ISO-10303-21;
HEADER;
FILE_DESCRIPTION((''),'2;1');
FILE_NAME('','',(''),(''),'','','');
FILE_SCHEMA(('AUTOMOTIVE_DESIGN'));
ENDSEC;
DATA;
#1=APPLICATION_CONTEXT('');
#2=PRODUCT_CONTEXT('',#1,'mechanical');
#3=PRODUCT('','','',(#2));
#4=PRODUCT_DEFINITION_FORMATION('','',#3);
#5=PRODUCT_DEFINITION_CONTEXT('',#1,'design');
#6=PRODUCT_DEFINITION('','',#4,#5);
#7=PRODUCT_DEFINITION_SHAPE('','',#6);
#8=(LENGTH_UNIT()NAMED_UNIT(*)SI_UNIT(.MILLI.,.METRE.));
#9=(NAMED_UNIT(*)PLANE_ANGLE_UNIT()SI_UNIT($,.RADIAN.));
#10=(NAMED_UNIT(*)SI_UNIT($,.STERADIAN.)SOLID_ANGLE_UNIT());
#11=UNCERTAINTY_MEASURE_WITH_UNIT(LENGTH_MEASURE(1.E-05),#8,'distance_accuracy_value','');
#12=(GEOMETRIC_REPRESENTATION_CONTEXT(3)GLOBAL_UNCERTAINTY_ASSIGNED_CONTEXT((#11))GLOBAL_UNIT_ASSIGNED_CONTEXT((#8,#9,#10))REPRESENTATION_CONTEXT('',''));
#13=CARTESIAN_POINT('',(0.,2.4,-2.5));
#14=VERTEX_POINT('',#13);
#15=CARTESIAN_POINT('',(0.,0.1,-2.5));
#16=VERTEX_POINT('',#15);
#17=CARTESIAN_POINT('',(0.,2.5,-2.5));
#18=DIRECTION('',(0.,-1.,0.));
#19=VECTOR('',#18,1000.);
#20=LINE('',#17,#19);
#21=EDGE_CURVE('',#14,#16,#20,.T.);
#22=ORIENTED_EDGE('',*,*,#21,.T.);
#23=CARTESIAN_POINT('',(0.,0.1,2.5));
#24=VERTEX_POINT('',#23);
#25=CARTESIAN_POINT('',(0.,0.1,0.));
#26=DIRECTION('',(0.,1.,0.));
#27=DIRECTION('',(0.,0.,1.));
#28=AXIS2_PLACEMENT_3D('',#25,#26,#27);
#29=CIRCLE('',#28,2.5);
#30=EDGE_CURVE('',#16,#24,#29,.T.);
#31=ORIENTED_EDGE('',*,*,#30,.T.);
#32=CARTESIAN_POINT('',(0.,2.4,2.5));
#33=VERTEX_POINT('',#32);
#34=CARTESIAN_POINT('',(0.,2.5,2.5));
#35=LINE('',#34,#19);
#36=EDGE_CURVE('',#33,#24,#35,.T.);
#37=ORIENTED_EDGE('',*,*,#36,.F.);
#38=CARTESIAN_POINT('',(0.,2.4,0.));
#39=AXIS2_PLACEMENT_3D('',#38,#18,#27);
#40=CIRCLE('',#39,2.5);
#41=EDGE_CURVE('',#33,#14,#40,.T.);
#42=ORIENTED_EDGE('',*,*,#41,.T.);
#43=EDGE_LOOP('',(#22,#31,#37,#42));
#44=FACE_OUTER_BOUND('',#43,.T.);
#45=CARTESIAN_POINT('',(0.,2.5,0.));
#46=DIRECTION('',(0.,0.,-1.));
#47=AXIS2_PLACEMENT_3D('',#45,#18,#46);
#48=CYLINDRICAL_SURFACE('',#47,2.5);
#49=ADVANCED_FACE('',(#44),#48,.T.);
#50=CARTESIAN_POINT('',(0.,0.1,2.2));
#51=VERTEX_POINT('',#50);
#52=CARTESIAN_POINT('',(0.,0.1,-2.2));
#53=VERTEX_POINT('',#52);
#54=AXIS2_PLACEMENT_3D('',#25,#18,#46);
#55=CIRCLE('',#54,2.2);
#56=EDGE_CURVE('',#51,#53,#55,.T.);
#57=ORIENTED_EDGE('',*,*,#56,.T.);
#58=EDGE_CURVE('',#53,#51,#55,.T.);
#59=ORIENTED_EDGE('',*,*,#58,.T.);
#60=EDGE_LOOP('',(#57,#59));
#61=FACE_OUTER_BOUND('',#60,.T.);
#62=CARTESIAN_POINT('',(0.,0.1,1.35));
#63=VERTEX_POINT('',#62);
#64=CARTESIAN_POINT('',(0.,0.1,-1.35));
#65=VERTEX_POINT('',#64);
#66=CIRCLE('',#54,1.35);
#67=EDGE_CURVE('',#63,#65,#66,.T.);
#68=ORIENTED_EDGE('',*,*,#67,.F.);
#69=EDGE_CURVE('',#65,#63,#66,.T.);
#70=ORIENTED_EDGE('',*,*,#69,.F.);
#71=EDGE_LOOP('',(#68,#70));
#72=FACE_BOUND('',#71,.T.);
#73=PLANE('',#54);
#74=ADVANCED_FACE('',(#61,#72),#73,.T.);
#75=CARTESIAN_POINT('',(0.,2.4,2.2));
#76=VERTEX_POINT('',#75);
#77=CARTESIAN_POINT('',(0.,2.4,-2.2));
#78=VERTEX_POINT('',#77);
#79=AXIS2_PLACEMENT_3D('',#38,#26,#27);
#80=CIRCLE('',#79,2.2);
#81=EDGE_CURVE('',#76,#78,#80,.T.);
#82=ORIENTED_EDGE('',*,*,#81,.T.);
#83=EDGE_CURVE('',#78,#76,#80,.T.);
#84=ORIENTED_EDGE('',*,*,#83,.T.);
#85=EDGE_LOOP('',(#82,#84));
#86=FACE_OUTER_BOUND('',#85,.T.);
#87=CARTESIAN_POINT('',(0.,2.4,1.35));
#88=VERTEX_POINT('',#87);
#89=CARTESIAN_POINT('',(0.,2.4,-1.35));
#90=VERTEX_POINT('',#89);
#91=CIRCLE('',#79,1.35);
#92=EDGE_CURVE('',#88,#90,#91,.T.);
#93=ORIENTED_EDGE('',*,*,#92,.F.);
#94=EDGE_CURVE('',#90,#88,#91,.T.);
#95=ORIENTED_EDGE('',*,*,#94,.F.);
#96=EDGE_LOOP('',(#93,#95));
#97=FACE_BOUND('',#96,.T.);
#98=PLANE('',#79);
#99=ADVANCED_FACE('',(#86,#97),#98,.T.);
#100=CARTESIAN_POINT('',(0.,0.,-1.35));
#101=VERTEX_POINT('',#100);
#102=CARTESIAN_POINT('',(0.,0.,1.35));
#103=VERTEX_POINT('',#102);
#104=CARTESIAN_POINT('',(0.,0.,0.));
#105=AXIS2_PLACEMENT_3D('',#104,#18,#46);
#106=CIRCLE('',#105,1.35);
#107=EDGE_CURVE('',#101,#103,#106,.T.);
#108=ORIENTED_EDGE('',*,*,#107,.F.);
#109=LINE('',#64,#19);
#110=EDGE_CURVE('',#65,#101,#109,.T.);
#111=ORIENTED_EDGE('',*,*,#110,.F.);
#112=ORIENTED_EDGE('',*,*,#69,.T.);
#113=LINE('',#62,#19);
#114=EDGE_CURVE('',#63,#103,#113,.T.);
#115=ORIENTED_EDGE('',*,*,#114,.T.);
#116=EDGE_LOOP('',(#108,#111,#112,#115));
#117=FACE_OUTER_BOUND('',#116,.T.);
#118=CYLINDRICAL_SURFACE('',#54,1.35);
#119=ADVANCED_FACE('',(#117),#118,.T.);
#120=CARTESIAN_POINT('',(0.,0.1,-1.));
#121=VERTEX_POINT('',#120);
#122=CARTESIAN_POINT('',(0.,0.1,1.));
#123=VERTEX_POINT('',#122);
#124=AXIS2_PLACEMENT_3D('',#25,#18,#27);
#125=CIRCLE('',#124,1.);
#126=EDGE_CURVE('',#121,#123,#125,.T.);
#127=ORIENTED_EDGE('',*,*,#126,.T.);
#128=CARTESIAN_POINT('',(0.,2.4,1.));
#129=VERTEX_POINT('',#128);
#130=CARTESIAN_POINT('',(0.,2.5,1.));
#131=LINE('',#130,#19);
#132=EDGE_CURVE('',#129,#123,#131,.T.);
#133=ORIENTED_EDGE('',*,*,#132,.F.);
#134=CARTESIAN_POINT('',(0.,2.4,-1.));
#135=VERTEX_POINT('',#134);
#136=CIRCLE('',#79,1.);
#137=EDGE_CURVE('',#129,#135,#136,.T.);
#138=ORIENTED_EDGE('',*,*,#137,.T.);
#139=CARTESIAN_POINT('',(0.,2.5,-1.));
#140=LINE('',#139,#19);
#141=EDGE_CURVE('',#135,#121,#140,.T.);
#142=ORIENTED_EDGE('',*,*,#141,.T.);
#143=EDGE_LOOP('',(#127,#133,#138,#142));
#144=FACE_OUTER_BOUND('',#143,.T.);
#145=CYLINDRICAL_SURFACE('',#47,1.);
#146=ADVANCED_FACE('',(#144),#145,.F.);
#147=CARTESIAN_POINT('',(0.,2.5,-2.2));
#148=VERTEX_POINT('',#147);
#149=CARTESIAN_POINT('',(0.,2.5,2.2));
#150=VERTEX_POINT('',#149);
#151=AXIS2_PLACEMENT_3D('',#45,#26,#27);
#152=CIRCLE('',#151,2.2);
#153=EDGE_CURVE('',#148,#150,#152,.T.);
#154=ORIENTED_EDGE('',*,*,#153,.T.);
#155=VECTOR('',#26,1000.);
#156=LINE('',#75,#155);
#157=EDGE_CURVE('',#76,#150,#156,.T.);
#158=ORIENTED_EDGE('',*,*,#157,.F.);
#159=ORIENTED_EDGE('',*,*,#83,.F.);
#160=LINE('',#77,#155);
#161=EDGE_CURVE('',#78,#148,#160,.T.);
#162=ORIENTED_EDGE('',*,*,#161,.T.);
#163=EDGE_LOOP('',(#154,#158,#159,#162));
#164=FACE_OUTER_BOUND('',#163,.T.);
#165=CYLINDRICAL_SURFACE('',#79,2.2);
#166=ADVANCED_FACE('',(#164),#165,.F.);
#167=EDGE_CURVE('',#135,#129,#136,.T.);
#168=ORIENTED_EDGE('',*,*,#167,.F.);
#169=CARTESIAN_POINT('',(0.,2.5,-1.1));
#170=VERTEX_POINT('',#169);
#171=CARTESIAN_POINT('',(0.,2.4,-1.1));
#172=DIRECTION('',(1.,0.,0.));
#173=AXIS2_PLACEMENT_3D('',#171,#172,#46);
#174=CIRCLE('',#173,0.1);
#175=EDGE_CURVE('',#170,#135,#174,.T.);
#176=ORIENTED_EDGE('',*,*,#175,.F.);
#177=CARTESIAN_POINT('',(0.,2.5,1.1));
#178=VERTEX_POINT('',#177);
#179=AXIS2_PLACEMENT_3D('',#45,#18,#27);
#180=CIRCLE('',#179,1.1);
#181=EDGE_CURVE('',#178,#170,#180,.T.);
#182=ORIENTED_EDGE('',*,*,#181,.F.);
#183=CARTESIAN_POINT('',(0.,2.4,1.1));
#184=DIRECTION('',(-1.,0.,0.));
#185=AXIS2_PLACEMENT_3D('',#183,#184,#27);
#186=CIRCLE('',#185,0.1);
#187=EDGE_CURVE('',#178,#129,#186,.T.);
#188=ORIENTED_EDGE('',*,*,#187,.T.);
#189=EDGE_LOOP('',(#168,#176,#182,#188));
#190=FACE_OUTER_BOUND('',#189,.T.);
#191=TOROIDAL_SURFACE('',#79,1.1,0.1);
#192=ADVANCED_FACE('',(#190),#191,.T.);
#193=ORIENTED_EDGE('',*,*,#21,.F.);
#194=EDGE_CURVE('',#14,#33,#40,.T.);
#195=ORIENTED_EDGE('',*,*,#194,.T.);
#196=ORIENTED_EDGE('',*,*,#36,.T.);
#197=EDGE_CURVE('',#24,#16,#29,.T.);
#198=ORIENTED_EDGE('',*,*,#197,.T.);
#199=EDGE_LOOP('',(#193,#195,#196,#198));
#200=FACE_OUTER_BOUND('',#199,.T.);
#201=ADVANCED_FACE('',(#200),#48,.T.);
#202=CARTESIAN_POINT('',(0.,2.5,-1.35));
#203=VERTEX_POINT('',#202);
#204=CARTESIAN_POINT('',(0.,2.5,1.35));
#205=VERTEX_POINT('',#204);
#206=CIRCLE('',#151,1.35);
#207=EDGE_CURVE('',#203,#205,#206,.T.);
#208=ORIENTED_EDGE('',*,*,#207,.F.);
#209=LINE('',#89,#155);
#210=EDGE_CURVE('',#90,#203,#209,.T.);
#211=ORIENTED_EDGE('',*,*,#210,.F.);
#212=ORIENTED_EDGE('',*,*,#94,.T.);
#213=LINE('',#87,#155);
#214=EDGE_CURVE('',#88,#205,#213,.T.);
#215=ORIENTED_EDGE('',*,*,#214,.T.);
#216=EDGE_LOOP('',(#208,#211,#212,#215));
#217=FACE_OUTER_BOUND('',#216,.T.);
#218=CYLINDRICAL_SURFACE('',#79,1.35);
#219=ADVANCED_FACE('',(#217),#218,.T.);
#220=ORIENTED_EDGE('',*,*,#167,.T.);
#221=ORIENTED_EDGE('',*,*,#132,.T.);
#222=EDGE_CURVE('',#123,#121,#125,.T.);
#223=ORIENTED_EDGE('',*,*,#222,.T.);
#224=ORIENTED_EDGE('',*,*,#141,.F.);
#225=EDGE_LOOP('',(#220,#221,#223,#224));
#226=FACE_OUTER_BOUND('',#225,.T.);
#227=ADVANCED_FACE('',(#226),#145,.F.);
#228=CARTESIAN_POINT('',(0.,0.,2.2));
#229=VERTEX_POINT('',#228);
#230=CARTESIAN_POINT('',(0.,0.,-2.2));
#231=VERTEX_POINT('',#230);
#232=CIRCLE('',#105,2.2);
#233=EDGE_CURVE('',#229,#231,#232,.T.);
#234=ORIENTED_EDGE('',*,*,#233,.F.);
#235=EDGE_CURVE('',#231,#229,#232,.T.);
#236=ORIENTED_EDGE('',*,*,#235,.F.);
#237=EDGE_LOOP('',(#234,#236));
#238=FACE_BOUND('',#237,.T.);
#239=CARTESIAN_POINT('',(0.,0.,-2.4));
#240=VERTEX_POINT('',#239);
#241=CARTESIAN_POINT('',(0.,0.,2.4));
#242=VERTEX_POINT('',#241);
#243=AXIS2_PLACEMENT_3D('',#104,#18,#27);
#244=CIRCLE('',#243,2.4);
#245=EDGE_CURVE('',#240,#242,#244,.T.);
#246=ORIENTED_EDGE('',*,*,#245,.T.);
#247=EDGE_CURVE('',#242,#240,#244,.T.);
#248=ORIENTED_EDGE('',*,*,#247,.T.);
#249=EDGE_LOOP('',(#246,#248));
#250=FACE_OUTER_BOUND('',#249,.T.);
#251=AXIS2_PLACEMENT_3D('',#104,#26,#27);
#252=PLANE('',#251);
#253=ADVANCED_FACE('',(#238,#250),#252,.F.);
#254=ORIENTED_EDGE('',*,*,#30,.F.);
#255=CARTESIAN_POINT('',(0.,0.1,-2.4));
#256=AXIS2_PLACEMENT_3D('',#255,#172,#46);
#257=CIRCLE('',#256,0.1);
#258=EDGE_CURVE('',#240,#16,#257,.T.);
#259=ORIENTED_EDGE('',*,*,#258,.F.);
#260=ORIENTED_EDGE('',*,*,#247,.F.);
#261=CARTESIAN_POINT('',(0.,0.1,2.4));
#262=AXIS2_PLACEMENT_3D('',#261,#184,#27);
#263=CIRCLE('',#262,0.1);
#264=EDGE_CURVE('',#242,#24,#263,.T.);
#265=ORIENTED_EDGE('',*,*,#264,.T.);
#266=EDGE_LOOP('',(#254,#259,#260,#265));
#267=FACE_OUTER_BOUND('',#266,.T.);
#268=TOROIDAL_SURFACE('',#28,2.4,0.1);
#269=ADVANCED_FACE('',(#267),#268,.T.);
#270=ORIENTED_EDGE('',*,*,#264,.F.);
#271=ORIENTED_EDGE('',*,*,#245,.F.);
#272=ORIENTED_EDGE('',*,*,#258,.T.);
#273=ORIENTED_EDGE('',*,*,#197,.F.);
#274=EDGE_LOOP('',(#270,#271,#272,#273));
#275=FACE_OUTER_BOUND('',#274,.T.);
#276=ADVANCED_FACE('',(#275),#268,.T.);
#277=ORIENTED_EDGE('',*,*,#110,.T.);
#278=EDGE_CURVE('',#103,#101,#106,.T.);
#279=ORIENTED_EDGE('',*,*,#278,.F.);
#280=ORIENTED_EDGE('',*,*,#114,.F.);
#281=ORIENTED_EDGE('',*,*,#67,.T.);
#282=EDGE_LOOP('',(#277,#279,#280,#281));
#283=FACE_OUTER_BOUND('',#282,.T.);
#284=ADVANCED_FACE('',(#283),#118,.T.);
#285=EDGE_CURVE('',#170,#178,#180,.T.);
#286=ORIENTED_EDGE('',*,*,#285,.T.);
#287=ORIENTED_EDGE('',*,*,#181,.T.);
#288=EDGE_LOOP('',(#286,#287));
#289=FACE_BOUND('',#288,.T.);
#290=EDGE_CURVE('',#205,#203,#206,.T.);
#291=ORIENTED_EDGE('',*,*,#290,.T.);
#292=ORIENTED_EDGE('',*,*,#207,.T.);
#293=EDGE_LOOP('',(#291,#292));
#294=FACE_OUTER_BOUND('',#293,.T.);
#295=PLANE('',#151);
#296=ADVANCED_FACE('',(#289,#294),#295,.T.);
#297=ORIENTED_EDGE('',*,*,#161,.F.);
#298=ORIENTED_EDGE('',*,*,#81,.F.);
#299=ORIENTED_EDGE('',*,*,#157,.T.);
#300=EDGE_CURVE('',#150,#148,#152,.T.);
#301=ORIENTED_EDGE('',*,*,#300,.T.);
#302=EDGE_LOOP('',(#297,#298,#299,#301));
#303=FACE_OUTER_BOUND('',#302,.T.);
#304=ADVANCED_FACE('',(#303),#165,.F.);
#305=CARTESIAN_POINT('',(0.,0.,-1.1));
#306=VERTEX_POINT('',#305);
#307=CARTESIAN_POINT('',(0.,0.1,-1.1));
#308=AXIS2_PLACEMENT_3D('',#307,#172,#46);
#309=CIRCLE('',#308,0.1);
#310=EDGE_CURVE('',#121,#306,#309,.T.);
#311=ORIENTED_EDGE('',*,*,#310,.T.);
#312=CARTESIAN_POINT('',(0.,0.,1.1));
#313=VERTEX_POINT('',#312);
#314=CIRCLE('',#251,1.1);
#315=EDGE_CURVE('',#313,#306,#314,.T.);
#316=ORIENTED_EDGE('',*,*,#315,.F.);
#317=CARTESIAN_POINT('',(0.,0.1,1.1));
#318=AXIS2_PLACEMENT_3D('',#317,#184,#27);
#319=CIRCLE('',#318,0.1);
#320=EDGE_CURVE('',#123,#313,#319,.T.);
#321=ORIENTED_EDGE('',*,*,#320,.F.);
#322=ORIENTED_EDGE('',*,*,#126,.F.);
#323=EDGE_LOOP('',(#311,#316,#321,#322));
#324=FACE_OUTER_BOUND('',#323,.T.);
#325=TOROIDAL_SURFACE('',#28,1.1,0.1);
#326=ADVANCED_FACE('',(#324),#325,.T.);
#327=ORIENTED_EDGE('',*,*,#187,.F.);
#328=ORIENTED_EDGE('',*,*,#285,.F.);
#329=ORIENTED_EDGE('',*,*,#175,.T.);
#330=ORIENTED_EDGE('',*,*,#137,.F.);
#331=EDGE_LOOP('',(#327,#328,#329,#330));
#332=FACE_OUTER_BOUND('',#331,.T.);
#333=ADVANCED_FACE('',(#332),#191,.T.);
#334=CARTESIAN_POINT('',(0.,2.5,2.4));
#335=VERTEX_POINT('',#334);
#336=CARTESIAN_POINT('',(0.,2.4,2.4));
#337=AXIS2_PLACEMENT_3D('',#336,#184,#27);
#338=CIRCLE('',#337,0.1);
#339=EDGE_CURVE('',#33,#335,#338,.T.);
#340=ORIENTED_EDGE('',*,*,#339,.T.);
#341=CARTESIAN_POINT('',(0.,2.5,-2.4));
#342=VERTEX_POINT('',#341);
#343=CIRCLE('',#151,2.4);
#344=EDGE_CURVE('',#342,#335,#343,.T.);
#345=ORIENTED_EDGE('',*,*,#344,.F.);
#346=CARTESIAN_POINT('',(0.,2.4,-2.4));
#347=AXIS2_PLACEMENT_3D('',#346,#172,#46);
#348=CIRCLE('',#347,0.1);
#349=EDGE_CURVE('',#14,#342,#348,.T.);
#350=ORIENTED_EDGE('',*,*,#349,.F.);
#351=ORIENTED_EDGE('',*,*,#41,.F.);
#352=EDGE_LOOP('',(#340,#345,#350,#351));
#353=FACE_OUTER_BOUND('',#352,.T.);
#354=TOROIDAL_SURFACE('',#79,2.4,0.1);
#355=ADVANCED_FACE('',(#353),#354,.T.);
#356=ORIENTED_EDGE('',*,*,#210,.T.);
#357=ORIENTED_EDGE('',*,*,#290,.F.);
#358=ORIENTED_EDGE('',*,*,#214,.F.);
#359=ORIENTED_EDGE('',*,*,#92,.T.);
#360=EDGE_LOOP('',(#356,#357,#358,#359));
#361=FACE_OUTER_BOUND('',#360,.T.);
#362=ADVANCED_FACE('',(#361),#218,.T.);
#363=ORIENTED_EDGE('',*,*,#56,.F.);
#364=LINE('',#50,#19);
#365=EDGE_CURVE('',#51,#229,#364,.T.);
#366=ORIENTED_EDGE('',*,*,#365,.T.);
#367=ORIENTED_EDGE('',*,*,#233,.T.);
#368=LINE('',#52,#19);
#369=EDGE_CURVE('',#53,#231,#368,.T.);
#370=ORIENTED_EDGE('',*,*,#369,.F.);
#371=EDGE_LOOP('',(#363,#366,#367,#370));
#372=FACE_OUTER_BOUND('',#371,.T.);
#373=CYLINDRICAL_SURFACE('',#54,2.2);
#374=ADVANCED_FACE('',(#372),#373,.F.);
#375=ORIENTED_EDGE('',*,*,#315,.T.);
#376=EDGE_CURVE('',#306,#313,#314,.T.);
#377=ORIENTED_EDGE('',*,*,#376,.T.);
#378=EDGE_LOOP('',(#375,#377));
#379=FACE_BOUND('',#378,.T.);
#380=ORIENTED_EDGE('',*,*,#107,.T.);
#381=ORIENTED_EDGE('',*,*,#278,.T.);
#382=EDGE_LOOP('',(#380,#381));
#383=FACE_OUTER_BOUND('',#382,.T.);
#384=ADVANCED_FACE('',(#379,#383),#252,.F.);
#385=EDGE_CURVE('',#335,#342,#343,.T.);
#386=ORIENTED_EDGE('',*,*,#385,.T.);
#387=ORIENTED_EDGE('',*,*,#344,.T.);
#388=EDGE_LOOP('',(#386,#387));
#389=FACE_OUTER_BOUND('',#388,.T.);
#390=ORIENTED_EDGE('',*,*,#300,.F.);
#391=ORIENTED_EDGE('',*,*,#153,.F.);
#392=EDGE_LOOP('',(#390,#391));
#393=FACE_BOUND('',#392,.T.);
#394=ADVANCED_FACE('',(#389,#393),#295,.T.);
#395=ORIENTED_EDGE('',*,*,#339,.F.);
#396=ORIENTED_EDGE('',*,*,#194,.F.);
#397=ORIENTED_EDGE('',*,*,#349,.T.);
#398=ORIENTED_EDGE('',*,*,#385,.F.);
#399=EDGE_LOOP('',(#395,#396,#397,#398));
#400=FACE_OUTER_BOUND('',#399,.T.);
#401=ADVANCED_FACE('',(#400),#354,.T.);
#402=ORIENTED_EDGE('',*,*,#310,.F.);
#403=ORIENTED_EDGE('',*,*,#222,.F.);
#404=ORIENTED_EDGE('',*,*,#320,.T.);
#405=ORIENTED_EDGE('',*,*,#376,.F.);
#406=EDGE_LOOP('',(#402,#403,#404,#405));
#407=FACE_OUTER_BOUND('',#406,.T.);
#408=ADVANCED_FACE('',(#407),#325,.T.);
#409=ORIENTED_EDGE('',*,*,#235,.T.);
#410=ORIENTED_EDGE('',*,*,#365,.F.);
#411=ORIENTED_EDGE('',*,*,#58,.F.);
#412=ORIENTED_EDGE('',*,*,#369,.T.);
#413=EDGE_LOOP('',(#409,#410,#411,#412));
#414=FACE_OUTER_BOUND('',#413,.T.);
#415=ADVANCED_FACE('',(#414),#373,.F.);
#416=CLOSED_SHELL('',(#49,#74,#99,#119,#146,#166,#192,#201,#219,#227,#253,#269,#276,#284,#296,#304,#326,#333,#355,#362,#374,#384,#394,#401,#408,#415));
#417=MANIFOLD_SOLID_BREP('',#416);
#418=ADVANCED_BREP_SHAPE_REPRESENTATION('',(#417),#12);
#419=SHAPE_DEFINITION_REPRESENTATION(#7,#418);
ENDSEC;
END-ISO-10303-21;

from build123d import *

# Parameters (mm, degrees)
SKETCH_1_R          = 2.5
SKETCH_1_R_2        = 1
EXTRUDE_1_DEPTH     = 2.5
SKETCH_2_R          = 2.2
SKETCH_2_R_2        = 1.35
CUT_EXTRUDE_1_DEPTH = 0.1
CUT_EXTRUDE_START   = -0.1
SKETCH_4_R          = 2.2
SKETCH_4_R_2        = 1.35
CUT_EXTRUDE_2_DEPTH = 0.1
FILLET_R0_1_1_R     = 0.1


with BuildPart() as part:
    # 草图1 → 凸台-拉伸1 (new body)
    with BuildSketch(Plane(origin=(0, 0, 0), x_dir=(1, 0, 0), z_dir=(0, 1, 0))):
        with Locations(Location((0, 0, 0), (0, 0, 270))):
            Circle(SKETCH_1_R)
        with Locations(Location((0, 0, 0), (0, 0, 270))):
            Circle(SKETCH_1_R_2, mode=Mode.SUBTRACT)
    extrude(amount=EXTRUDE_1_DEPTH)

    # 草图2 → 切除-拉伸1 (cut)
    with BuildSketch(Plane(origin=(0, 2.5, 0), x_dir=(1, 0, 0), z_dir=(0, 1, 0))):
        with Locations(Location((0, 0, 0), (0, 0, 270))):
            Circle(SKETCH_2_R)
        with Locations(Location((0, 0, 0), (0, 0, 270))):
            Circle(SKETCH_2_R_2, mode=Mode.SUBTRACT)
    extrude(amount=-CUT_EXTRUDE_1_DEPTH, mode=Mode.SUBTRACT)

    # 草图4 → 切除-拉伸2 (cut)
    with BuildSketch(Plane.XZ.offset(CUT_EXTRUDE_START)):
        with Locations(Location((0, 0, 0), (0, 0, 90))):
            Circle(SKETCH_4_R)
        with Locations(Location((0, 0, 0), (0, 0, 90))):
            Circle(SKETCH_4_R_2, mode=Mode.SUBTRACT)
    extrude(amount=CUT_EXTRUDE_2_DEPTH, mode=Mode.SUBTRACT)

    # R0.1 圆角1
    fillet_r0_1_1_edges = [part.edges().sort_by_distance(p)[0] for p in [
        (0, 0, -2.5),
        (0, 2.5, -2.5),
        (0, 0, -1),
        (0, 2.5, -1),
    ]]
    fillet(fillet_r0_1_1_edges, radius=FILLET_R0_1_1_R)


solid = part.part
